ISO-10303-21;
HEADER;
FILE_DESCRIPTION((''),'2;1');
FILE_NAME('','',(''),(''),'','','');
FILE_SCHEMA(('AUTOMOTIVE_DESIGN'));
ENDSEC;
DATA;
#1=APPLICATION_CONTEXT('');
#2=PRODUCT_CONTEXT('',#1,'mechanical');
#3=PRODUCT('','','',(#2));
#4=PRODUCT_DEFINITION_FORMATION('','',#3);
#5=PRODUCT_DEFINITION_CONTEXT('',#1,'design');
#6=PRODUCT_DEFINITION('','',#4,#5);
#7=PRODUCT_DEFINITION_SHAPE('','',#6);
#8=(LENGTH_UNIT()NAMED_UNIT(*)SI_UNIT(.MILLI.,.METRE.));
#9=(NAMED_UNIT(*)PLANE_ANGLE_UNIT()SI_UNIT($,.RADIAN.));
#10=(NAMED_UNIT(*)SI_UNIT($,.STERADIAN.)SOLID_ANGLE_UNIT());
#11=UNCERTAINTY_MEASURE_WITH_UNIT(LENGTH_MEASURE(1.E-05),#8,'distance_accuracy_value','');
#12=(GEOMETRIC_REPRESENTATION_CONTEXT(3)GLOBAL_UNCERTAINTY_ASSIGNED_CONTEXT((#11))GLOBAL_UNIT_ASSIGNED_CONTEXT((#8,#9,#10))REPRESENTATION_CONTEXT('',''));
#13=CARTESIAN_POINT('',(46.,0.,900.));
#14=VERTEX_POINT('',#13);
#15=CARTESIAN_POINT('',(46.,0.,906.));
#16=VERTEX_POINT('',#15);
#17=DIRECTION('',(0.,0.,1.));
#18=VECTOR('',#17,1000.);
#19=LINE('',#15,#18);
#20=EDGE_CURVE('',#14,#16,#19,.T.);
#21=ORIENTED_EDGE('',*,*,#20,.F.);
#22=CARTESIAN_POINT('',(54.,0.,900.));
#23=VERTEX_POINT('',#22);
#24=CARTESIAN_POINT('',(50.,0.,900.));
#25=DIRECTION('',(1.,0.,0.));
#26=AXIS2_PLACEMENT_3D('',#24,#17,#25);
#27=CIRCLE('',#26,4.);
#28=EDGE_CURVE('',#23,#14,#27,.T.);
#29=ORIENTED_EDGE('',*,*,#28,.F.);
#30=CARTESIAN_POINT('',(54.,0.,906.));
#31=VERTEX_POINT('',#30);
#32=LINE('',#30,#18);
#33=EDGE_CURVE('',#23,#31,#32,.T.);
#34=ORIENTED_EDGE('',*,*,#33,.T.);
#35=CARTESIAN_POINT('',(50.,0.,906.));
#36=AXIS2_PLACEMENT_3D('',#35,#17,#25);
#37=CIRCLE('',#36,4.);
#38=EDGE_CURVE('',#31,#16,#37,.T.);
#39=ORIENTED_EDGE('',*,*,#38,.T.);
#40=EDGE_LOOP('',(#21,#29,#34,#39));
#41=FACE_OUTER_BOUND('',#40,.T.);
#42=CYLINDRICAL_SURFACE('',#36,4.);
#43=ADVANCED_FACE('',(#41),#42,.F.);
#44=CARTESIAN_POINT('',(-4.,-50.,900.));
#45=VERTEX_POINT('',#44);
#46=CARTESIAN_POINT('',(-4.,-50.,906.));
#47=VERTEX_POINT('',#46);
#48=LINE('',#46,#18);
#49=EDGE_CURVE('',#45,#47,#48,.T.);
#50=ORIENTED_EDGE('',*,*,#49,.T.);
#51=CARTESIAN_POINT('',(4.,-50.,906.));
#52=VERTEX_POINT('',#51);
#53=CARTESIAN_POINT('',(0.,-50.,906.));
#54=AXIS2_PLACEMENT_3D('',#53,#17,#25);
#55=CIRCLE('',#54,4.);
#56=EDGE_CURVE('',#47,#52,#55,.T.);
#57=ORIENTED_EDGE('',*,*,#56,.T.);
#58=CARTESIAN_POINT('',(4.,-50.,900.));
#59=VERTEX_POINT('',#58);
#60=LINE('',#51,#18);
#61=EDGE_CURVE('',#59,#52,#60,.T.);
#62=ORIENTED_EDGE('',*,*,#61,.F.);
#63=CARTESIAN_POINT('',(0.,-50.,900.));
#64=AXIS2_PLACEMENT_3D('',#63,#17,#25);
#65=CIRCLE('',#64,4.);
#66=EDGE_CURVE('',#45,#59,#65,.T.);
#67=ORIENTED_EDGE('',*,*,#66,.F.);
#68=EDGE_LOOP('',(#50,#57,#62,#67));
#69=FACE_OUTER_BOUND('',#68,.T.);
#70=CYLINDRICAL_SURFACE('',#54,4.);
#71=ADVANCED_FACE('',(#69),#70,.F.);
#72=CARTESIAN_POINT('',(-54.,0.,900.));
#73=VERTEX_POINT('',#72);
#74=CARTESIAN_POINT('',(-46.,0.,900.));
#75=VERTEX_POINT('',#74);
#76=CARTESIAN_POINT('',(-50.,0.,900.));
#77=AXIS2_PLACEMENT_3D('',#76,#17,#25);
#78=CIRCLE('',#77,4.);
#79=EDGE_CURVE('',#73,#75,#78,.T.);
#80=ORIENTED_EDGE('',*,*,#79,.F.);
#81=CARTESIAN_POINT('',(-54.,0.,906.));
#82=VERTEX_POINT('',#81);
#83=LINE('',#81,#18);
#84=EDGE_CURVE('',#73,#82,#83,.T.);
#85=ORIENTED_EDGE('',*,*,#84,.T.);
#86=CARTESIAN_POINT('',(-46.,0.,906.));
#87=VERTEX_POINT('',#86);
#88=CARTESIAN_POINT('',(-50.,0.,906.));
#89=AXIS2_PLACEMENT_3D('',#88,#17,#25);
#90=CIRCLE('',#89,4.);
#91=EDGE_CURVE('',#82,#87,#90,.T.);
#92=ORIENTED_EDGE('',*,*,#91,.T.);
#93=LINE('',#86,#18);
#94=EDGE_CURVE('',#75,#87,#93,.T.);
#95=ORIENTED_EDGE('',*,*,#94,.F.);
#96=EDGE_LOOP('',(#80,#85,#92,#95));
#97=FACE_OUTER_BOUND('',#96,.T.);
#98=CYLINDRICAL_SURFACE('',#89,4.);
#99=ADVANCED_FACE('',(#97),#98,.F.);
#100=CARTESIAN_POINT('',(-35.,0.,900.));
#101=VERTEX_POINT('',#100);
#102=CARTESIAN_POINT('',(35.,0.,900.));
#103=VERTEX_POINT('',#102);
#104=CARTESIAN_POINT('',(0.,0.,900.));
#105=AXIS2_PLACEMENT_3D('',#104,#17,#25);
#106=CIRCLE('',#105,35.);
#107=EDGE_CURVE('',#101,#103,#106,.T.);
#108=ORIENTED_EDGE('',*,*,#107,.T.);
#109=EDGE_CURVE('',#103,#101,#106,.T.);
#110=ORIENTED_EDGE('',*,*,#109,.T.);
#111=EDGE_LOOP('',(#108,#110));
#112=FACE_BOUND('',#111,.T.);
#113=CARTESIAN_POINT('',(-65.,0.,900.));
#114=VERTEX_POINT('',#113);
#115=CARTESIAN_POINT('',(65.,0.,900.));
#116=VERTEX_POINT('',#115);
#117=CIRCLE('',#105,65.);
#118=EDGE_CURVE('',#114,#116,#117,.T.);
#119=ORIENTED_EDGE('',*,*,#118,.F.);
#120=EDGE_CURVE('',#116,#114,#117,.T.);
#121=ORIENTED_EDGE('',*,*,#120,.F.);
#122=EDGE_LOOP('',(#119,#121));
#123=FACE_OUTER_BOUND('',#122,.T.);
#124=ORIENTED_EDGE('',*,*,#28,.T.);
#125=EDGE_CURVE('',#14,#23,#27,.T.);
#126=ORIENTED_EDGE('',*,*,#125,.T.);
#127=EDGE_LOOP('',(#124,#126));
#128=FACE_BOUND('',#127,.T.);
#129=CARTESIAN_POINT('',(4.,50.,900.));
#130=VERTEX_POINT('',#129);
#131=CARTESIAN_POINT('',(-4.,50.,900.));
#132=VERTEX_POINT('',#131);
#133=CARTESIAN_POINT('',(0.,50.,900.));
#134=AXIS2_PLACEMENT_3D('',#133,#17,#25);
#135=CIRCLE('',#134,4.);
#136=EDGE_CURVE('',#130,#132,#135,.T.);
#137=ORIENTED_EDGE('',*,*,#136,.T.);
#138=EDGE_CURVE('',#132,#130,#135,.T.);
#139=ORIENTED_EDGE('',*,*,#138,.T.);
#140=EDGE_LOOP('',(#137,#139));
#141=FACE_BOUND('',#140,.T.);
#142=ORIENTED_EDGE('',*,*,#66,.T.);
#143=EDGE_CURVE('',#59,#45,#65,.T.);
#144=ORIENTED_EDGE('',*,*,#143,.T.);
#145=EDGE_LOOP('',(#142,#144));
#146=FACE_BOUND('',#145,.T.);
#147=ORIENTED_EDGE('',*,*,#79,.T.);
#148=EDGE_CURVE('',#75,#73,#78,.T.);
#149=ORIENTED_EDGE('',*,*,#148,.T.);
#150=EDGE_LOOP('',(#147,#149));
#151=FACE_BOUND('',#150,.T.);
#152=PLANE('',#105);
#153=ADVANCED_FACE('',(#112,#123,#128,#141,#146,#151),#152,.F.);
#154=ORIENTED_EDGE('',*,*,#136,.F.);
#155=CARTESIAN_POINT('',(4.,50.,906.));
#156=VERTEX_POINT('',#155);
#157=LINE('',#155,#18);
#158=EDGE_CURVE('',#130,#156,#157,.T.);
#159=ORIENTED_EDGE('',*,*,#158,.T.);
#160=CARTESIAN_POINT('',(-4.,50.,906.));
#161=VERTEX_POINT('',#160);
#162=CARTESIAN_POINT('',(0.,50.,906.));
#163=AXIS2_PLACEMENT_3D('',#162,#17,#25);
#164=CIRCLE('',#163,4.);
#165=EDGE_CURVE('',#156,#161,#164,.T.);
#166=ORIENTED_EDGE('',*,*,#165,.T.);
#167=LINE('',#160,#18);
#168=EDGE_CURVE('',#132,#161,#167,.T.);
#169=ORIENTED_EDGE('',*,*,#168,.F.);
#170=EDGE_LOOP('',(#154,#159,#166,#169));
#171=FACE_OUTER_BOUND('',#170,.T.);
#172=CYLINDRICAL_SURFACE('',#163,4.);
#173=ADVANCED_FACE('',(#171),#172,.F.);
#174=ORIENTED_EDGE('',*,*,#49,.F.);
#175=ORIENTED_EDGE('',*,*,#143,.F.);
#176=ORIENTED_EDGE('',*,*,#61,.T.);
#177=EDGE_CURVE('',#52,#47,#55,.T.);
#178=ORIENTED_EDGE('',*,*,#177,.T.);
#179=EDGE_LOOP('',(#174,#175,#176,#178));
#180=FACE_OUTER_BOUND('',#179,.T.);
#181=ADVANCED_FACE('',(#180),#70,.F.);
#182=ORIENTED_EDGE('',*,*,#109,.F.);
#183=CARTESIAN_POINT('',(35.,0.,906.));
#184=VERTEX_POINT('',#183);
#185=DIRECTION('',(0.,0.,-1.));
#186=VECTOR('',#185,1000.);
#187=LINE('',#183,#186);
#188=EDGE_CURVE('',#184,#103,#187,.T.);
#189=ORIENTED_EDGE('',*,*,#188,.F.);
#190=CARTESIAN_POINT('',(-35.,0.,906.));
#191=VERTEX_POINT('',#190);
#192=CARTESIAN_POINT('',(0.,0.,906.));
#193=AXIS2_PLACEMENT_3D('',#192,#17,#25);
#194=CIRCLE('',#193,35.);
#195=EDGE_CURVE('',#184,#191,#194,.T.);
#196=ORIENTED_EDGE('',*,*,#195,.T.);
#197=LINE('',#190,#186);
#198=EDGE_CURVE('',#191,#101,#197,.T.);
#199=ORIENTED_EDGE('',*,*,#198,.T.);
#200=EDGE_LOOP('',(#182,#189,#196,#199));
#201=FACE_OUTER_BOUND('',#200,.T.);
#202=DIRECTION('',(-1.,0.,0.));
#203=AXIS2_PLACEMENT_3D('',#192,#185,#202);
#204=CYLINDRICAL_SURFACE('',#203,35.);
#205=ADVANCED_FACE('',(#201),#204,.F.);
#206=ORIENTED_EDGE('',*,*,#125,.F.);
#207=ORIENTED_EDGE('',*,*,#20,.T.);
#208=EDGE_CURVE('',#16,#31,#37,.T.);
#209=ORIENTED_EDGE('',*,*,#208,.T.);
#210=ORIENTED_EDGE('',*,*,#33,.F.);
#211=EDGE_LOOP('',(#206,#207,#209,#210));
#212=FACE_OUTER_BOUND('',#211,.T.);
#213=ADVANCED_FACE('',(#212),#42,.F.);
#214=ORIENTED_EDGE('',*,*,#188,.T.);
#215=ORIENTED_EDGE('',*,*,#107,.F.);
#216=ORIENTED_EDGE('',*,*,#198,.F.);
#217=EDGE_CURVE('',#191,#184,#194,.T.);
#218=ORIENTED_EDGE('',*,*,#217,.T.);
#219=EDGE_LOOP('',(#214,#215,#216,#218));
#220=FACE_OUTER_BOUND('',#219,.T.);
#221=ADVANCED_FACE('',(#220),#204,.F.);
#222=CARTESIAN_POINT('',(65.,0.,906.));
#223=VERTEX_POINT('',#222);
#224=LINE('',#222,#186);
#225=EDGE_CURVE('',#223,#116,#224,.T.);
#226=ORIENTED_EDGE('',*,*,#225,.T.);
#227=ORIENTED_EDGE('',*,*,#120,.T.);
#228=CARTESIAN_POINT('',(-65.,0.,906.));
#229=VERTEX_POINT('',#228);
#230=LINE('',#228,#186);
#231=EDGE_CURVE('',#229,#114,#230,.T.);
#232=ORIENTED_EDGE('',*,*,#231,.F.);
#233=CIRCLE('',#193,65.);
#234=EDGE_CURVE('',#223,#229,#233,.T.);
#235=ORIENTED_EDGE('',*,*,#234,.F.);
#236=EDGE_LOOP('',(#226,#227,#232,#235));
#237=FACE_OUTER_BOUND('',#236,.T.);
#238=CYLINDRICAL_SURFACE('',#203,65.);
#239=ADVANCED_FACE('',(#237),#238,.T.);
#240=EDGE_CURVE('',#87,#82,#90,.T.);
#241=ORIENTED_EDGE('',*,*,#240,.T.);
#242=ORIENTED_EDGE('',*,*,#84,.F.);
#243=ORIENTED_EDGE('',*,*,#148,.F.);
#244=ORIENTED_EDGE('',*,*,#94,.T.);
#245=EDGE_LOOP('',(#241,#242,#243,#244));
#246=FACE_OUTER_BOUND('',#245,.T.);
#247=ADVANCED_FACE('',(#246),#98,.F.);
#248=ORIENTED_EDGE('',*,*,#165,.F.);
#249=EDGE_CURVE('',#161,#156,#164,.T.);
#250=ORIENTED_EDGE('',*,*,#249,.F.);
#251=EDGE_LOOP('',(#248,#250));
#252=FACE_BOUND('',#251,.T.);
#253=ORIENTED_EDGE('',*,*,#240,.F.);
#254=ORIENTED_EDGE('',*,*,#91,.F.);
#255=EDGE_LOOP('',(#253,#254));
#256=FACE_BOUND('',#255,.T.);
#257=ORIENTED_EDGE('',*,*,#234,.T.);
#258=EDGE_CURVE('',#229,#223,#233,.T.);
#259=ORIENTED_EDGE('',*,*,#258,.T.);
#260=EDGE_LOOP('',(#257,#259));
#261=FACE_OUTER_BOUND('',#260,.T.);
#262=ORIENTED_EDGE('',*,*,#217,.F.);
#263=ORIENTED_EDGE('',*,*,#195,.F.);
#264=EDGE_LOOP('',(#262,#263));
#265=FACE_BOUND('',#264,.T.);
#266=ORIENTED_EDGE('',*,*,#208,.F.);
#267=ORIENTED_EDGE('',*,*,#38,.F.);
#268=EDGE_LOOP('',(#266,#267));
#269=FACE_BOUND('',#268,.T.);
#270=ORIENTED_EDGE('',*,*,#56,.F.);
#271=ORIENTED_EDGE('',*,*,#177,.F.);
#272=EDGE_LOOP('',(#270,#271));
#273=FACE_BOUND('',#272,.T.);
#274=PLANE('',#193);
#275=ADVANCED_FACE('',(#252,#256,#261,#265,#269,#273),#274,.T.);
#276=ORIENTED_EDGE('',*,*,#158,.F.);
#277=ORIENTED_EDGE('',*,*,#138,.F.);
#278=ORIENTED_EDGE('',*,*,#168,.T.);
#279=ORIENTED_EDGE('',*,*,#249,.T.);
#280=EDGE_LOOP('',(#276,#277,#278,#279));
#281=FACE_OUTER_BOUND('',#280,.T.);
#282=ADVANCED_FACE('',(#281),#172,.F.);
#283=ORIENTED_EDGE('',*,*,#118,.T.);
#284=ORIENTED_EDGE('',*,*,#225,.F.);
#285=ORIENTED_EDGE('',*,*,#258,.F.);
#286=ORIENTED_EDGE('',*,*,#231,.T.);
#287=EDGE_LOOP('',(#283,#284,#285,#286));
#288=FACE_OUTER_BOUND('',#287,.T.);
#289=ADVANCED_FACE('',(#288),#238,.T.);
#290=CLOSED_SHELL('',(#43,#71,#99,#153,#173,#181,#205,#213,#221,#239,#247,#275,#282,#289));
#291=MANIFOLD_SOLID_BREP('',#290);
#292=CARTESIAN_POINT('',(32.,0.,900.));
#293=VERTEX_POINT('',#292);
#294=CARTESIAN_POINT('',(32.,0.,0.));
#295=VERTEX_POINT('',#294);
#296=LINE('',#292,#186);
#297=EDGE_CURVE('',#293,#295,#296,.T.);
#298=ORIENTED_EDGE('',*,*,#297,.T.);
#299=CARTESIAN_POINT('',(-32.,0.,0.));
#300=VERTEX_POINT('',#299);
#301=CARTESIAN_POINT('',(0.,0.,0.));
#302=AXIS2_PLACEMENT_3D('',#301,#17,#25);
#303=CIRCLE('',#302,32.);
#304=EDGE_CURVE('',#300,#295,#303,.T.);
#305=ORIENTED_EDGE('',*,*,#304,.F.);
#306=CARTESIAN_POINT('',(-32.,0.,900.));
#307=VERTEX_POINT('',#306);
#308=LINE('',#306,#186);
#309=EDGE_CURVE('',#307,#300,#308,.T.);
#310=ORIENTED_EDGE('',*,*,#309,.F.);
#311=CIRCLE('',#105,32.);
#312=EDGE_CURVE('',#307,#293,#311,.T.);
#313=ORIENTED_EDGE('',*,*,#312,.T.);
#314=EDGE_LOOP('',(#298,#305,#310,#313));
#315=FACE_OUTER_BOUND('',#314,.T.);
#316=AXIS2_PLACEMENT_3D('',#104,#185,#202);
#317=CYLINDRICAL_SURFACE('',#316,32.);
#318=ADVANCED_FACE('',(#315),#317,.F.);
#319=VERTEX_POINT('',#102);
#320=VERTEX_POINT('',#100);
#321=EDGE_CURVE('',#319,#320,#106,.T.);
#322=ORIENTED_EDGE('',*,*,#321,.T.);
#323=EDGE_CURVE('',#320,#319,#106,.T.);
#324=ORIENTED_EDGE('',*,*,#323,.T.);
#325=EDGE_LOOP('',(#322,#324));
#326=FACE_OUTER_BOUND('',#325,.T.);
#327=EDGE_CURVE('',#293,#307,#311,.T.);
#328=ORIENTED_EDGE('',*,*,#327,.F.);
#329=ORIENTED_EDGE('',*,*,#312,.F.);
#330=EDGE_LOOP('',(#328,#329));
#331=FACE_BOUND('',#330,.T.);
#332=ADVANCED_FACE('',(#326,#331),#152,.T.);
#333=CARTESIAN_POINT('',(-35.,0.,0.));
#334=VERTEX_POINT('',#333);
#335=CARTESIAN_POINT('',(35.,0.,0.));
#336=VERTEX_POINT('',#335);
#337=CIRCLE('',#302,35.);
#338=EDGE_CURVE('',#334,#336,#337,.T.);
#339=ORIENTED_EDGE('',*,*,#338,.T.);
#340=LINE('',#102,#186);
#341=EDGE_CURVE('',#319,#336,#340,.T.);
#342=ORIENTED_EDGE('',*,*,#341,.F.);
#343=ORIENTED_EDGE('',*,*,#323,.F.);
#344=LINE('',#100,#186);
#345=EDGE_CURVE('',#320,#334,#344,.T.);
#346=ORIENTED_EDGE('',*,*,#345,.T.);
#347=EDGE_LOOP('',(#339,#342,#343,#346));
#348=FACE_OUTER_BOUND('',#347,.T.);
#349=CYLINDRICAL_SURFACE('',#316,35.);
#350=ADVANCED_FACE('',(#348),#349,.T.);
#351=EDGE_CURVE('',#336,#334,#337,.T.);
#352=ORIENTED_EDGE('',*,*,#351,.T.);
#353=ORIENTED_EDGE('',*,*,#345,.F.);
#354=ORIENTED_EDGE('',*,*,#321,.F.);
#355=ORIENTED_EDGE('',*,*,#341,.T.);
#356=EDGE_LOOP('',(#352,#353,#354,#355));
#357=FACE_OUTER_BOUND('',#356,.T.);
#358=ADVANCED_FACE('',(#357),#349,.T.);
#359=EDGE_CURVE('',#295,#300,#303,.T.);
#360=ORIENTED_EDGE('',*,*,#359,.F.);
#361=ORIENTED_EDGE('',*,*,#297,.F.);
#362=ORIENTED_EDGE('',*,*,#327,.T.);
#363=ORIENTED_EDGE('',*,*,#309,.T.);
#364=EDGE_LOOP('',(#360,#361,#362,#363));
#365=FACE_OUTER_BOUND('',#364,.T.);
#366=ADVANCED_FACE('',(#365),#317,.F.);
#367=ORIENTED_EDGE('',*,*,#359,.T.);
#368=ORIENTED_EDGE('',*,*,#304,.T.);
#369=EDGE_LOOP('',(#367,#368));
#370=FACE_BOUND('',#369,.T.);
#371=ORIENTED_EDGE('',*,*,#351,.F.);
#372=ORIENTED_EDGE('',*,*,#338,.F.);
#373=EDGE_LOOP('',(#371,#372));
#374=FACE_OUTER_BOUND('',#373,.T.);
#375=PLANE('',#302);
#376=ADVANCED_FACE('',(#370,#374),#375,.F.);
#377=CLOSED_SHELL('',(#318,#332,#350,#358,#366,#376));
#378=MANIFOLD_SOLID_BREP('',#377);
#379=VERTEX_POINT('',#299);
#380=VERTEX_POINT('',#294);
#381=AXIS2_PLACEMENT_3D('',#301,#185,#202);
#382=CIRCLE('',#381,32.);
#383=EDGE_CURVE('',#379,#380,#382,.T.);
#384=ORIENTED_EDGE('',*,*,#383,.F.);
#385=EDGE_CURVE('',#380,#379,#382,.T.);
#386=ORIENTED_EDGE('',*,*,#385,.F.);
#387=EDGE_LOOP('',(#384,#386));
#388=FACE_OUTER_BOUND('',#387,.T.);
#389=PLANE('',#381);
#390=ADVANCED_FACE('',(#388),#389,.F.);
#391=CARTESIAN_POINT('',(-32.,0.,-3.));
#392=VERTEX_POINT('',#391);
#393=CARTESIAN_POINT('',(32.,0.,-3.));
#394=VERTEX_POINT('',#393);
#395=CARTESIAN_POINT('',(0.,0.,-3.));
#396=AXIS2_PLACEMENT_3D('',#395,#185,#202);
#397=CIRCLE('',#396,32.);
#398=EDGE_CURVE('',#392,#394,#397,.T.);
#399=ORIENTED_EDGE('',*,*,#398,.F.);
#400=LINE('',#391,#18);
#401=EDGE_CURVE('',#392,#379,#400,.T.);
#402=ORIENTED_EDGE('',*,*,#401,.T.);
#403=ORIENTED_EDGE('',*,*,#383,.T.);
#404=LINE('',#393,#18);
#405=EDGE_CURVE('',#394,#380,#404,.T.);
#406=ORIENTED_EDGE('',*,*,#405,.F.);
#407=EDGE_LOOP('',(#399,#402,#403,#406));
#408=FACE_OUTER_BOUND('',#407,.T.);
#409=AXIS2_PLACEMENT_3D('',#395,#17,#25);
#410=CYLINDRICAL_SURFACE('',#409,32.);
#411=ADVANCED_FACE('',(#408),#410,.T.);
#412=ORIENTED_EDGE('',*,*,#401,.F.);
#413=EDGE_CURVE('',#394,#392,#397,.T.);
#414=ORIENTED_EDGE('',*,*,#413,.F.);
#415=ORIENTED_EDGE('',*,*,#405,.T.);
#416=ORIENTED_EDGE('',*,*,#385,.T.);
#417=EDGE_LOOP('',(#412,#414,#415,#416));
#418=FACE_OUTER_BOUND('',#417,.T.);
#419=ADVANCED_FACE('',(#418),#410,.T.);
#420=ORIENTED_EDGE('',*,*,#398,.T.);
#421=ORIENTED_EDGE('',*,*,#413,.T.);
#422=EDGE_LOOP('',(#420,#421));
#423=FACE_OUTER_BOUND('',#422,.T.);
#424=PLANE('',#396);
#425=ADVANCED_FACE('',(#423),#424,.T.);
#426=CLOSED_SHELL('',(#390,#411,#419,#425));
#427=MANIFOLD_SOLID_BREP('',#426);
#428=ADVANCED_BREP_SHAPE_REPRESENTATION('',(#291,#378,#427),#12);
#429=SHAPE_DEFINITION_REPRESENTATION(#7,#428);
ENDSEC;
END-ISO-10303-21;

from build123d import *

# Parameters (mm, degrees)
SKETCH1_R                = 35
SKETCH1_R_2              = 32
THIN_EXTRUDE1_DEPTH      = 900
SKETCH3_R                = 32
BOSS_EXTRUDE1_DEPTH      = 3
SKETCH4_R                = 65
SKETCH4_R_2              = 35
BOSS_EXTRUDE2_DEPTH      = 6
SKETCH6_W                = 4
SKETCH6_H                = 6.001
F_8_0_8_HOLE1_AT_2_COUNT = 2
F_8_0_8_HOLE1_AT_2_PITCH = 70.710678119
F_8_0_8_HOLE1_AT_3_COUNT = 2
F_8_0_8_HOLE1_AT_3_PITCH = 100
F_8_0_8_HOLE1_AT_4_COUNT = 2
F_8_0_8_HOLE1_AT_4_PITCH = 70.710678119


with BuildPart() as part:
    # Sketch1 → Thin Extrude1 (new body)
    with BuildSketch(Plane.XY):
        Circle(SKETCH1_R)
        Circle(SKETCH1_R_2, mode=Mode.SUBTRACT)
    extrude(amount=THIN_EXTRUDE1_DEPTH)


with BuildPart() as body_2:
    # Sketch3 → Boss-Extrude1 (new body)
    with BuildSketch(Plane(origin=(0, 0, 0), x_dir=(-1, 0, 0), z_dir=(0, 0, -1))):
        Circle(SKETCH3_R)
    extrude(amount=BOSS_EXTRUDE1_DEPTH)


with BuildPart() as body_3:
    # Sketch4 → Boss-Extrude2 (new body)
    with BuildSketch(Plane.XY.offset(900)):
        Circle(SKETCH4_R)
        Circle(SKETCH4_R_2, mode=Mode.SUBTRACT)
    extrude(amount=BOSS_EXTRUDE2_DEPTH)

    # Sketch6 → Ø8.0 (8) Hole1 (revolve, cut)
    with BuildSketch(Plane(origin=(0, 50, 906), x_dir=(0, -1, 0), z_dir=(1, 0, 0))):
        with Locations((2, 3.0005)):
            Rectangle(SKETCH6_W, SKETCH6_H)
    f_8_0_8_hole1 = revolve(axis=Axis((0, 50, 912.35), (0, 0, -1)), mode=Mode.SUBTRACT)

    # Ø8.0 (8) Hole1 at 2: Ø8.0 (8) Hole1 ×2
    with Locations(*[Vector(-0.7071067811865476, -0.7071067811865476, 0) * (i * F_8_0_8_HOLE1_AT_2_PITCH) for i in range(1, F_8_0_8_HOLE1_AT_2_COUNT)]):
        add(f_8_0_8_hole1, mode=Mode.SUBTRACT)

    # Ø8.0 (8) Hole1 at 3: Ø8.0 (8) Hole1 ×2
    with Locations(*[(0, -i * F_8_0_8_HOLE1_AT_3_PITCH, 0) for i in range(1, F_8_0_8_HOLE1_AT_3_COUNT)]):
        add(f_8_0_8_hole1, mode=Mode.SUBTRACT)

    # Ø8.0 (8) Hole1 at 4: Ø8.0 (8) Hole1 ×2
    with Locations(*[Vector(0.7071067811865476, -0.7071067811865476, 0) * (i * F_8_0_8_HOLE1_AT_4_PITCH) for i in range(1, F_8_0_8_HOLE1_AT_4_COUNT)]):
        add(f_8_0_8_hole1, mode=Mode.SUBTRACT)


solid = Compound([part.part, body_2.part, body_3.part])
